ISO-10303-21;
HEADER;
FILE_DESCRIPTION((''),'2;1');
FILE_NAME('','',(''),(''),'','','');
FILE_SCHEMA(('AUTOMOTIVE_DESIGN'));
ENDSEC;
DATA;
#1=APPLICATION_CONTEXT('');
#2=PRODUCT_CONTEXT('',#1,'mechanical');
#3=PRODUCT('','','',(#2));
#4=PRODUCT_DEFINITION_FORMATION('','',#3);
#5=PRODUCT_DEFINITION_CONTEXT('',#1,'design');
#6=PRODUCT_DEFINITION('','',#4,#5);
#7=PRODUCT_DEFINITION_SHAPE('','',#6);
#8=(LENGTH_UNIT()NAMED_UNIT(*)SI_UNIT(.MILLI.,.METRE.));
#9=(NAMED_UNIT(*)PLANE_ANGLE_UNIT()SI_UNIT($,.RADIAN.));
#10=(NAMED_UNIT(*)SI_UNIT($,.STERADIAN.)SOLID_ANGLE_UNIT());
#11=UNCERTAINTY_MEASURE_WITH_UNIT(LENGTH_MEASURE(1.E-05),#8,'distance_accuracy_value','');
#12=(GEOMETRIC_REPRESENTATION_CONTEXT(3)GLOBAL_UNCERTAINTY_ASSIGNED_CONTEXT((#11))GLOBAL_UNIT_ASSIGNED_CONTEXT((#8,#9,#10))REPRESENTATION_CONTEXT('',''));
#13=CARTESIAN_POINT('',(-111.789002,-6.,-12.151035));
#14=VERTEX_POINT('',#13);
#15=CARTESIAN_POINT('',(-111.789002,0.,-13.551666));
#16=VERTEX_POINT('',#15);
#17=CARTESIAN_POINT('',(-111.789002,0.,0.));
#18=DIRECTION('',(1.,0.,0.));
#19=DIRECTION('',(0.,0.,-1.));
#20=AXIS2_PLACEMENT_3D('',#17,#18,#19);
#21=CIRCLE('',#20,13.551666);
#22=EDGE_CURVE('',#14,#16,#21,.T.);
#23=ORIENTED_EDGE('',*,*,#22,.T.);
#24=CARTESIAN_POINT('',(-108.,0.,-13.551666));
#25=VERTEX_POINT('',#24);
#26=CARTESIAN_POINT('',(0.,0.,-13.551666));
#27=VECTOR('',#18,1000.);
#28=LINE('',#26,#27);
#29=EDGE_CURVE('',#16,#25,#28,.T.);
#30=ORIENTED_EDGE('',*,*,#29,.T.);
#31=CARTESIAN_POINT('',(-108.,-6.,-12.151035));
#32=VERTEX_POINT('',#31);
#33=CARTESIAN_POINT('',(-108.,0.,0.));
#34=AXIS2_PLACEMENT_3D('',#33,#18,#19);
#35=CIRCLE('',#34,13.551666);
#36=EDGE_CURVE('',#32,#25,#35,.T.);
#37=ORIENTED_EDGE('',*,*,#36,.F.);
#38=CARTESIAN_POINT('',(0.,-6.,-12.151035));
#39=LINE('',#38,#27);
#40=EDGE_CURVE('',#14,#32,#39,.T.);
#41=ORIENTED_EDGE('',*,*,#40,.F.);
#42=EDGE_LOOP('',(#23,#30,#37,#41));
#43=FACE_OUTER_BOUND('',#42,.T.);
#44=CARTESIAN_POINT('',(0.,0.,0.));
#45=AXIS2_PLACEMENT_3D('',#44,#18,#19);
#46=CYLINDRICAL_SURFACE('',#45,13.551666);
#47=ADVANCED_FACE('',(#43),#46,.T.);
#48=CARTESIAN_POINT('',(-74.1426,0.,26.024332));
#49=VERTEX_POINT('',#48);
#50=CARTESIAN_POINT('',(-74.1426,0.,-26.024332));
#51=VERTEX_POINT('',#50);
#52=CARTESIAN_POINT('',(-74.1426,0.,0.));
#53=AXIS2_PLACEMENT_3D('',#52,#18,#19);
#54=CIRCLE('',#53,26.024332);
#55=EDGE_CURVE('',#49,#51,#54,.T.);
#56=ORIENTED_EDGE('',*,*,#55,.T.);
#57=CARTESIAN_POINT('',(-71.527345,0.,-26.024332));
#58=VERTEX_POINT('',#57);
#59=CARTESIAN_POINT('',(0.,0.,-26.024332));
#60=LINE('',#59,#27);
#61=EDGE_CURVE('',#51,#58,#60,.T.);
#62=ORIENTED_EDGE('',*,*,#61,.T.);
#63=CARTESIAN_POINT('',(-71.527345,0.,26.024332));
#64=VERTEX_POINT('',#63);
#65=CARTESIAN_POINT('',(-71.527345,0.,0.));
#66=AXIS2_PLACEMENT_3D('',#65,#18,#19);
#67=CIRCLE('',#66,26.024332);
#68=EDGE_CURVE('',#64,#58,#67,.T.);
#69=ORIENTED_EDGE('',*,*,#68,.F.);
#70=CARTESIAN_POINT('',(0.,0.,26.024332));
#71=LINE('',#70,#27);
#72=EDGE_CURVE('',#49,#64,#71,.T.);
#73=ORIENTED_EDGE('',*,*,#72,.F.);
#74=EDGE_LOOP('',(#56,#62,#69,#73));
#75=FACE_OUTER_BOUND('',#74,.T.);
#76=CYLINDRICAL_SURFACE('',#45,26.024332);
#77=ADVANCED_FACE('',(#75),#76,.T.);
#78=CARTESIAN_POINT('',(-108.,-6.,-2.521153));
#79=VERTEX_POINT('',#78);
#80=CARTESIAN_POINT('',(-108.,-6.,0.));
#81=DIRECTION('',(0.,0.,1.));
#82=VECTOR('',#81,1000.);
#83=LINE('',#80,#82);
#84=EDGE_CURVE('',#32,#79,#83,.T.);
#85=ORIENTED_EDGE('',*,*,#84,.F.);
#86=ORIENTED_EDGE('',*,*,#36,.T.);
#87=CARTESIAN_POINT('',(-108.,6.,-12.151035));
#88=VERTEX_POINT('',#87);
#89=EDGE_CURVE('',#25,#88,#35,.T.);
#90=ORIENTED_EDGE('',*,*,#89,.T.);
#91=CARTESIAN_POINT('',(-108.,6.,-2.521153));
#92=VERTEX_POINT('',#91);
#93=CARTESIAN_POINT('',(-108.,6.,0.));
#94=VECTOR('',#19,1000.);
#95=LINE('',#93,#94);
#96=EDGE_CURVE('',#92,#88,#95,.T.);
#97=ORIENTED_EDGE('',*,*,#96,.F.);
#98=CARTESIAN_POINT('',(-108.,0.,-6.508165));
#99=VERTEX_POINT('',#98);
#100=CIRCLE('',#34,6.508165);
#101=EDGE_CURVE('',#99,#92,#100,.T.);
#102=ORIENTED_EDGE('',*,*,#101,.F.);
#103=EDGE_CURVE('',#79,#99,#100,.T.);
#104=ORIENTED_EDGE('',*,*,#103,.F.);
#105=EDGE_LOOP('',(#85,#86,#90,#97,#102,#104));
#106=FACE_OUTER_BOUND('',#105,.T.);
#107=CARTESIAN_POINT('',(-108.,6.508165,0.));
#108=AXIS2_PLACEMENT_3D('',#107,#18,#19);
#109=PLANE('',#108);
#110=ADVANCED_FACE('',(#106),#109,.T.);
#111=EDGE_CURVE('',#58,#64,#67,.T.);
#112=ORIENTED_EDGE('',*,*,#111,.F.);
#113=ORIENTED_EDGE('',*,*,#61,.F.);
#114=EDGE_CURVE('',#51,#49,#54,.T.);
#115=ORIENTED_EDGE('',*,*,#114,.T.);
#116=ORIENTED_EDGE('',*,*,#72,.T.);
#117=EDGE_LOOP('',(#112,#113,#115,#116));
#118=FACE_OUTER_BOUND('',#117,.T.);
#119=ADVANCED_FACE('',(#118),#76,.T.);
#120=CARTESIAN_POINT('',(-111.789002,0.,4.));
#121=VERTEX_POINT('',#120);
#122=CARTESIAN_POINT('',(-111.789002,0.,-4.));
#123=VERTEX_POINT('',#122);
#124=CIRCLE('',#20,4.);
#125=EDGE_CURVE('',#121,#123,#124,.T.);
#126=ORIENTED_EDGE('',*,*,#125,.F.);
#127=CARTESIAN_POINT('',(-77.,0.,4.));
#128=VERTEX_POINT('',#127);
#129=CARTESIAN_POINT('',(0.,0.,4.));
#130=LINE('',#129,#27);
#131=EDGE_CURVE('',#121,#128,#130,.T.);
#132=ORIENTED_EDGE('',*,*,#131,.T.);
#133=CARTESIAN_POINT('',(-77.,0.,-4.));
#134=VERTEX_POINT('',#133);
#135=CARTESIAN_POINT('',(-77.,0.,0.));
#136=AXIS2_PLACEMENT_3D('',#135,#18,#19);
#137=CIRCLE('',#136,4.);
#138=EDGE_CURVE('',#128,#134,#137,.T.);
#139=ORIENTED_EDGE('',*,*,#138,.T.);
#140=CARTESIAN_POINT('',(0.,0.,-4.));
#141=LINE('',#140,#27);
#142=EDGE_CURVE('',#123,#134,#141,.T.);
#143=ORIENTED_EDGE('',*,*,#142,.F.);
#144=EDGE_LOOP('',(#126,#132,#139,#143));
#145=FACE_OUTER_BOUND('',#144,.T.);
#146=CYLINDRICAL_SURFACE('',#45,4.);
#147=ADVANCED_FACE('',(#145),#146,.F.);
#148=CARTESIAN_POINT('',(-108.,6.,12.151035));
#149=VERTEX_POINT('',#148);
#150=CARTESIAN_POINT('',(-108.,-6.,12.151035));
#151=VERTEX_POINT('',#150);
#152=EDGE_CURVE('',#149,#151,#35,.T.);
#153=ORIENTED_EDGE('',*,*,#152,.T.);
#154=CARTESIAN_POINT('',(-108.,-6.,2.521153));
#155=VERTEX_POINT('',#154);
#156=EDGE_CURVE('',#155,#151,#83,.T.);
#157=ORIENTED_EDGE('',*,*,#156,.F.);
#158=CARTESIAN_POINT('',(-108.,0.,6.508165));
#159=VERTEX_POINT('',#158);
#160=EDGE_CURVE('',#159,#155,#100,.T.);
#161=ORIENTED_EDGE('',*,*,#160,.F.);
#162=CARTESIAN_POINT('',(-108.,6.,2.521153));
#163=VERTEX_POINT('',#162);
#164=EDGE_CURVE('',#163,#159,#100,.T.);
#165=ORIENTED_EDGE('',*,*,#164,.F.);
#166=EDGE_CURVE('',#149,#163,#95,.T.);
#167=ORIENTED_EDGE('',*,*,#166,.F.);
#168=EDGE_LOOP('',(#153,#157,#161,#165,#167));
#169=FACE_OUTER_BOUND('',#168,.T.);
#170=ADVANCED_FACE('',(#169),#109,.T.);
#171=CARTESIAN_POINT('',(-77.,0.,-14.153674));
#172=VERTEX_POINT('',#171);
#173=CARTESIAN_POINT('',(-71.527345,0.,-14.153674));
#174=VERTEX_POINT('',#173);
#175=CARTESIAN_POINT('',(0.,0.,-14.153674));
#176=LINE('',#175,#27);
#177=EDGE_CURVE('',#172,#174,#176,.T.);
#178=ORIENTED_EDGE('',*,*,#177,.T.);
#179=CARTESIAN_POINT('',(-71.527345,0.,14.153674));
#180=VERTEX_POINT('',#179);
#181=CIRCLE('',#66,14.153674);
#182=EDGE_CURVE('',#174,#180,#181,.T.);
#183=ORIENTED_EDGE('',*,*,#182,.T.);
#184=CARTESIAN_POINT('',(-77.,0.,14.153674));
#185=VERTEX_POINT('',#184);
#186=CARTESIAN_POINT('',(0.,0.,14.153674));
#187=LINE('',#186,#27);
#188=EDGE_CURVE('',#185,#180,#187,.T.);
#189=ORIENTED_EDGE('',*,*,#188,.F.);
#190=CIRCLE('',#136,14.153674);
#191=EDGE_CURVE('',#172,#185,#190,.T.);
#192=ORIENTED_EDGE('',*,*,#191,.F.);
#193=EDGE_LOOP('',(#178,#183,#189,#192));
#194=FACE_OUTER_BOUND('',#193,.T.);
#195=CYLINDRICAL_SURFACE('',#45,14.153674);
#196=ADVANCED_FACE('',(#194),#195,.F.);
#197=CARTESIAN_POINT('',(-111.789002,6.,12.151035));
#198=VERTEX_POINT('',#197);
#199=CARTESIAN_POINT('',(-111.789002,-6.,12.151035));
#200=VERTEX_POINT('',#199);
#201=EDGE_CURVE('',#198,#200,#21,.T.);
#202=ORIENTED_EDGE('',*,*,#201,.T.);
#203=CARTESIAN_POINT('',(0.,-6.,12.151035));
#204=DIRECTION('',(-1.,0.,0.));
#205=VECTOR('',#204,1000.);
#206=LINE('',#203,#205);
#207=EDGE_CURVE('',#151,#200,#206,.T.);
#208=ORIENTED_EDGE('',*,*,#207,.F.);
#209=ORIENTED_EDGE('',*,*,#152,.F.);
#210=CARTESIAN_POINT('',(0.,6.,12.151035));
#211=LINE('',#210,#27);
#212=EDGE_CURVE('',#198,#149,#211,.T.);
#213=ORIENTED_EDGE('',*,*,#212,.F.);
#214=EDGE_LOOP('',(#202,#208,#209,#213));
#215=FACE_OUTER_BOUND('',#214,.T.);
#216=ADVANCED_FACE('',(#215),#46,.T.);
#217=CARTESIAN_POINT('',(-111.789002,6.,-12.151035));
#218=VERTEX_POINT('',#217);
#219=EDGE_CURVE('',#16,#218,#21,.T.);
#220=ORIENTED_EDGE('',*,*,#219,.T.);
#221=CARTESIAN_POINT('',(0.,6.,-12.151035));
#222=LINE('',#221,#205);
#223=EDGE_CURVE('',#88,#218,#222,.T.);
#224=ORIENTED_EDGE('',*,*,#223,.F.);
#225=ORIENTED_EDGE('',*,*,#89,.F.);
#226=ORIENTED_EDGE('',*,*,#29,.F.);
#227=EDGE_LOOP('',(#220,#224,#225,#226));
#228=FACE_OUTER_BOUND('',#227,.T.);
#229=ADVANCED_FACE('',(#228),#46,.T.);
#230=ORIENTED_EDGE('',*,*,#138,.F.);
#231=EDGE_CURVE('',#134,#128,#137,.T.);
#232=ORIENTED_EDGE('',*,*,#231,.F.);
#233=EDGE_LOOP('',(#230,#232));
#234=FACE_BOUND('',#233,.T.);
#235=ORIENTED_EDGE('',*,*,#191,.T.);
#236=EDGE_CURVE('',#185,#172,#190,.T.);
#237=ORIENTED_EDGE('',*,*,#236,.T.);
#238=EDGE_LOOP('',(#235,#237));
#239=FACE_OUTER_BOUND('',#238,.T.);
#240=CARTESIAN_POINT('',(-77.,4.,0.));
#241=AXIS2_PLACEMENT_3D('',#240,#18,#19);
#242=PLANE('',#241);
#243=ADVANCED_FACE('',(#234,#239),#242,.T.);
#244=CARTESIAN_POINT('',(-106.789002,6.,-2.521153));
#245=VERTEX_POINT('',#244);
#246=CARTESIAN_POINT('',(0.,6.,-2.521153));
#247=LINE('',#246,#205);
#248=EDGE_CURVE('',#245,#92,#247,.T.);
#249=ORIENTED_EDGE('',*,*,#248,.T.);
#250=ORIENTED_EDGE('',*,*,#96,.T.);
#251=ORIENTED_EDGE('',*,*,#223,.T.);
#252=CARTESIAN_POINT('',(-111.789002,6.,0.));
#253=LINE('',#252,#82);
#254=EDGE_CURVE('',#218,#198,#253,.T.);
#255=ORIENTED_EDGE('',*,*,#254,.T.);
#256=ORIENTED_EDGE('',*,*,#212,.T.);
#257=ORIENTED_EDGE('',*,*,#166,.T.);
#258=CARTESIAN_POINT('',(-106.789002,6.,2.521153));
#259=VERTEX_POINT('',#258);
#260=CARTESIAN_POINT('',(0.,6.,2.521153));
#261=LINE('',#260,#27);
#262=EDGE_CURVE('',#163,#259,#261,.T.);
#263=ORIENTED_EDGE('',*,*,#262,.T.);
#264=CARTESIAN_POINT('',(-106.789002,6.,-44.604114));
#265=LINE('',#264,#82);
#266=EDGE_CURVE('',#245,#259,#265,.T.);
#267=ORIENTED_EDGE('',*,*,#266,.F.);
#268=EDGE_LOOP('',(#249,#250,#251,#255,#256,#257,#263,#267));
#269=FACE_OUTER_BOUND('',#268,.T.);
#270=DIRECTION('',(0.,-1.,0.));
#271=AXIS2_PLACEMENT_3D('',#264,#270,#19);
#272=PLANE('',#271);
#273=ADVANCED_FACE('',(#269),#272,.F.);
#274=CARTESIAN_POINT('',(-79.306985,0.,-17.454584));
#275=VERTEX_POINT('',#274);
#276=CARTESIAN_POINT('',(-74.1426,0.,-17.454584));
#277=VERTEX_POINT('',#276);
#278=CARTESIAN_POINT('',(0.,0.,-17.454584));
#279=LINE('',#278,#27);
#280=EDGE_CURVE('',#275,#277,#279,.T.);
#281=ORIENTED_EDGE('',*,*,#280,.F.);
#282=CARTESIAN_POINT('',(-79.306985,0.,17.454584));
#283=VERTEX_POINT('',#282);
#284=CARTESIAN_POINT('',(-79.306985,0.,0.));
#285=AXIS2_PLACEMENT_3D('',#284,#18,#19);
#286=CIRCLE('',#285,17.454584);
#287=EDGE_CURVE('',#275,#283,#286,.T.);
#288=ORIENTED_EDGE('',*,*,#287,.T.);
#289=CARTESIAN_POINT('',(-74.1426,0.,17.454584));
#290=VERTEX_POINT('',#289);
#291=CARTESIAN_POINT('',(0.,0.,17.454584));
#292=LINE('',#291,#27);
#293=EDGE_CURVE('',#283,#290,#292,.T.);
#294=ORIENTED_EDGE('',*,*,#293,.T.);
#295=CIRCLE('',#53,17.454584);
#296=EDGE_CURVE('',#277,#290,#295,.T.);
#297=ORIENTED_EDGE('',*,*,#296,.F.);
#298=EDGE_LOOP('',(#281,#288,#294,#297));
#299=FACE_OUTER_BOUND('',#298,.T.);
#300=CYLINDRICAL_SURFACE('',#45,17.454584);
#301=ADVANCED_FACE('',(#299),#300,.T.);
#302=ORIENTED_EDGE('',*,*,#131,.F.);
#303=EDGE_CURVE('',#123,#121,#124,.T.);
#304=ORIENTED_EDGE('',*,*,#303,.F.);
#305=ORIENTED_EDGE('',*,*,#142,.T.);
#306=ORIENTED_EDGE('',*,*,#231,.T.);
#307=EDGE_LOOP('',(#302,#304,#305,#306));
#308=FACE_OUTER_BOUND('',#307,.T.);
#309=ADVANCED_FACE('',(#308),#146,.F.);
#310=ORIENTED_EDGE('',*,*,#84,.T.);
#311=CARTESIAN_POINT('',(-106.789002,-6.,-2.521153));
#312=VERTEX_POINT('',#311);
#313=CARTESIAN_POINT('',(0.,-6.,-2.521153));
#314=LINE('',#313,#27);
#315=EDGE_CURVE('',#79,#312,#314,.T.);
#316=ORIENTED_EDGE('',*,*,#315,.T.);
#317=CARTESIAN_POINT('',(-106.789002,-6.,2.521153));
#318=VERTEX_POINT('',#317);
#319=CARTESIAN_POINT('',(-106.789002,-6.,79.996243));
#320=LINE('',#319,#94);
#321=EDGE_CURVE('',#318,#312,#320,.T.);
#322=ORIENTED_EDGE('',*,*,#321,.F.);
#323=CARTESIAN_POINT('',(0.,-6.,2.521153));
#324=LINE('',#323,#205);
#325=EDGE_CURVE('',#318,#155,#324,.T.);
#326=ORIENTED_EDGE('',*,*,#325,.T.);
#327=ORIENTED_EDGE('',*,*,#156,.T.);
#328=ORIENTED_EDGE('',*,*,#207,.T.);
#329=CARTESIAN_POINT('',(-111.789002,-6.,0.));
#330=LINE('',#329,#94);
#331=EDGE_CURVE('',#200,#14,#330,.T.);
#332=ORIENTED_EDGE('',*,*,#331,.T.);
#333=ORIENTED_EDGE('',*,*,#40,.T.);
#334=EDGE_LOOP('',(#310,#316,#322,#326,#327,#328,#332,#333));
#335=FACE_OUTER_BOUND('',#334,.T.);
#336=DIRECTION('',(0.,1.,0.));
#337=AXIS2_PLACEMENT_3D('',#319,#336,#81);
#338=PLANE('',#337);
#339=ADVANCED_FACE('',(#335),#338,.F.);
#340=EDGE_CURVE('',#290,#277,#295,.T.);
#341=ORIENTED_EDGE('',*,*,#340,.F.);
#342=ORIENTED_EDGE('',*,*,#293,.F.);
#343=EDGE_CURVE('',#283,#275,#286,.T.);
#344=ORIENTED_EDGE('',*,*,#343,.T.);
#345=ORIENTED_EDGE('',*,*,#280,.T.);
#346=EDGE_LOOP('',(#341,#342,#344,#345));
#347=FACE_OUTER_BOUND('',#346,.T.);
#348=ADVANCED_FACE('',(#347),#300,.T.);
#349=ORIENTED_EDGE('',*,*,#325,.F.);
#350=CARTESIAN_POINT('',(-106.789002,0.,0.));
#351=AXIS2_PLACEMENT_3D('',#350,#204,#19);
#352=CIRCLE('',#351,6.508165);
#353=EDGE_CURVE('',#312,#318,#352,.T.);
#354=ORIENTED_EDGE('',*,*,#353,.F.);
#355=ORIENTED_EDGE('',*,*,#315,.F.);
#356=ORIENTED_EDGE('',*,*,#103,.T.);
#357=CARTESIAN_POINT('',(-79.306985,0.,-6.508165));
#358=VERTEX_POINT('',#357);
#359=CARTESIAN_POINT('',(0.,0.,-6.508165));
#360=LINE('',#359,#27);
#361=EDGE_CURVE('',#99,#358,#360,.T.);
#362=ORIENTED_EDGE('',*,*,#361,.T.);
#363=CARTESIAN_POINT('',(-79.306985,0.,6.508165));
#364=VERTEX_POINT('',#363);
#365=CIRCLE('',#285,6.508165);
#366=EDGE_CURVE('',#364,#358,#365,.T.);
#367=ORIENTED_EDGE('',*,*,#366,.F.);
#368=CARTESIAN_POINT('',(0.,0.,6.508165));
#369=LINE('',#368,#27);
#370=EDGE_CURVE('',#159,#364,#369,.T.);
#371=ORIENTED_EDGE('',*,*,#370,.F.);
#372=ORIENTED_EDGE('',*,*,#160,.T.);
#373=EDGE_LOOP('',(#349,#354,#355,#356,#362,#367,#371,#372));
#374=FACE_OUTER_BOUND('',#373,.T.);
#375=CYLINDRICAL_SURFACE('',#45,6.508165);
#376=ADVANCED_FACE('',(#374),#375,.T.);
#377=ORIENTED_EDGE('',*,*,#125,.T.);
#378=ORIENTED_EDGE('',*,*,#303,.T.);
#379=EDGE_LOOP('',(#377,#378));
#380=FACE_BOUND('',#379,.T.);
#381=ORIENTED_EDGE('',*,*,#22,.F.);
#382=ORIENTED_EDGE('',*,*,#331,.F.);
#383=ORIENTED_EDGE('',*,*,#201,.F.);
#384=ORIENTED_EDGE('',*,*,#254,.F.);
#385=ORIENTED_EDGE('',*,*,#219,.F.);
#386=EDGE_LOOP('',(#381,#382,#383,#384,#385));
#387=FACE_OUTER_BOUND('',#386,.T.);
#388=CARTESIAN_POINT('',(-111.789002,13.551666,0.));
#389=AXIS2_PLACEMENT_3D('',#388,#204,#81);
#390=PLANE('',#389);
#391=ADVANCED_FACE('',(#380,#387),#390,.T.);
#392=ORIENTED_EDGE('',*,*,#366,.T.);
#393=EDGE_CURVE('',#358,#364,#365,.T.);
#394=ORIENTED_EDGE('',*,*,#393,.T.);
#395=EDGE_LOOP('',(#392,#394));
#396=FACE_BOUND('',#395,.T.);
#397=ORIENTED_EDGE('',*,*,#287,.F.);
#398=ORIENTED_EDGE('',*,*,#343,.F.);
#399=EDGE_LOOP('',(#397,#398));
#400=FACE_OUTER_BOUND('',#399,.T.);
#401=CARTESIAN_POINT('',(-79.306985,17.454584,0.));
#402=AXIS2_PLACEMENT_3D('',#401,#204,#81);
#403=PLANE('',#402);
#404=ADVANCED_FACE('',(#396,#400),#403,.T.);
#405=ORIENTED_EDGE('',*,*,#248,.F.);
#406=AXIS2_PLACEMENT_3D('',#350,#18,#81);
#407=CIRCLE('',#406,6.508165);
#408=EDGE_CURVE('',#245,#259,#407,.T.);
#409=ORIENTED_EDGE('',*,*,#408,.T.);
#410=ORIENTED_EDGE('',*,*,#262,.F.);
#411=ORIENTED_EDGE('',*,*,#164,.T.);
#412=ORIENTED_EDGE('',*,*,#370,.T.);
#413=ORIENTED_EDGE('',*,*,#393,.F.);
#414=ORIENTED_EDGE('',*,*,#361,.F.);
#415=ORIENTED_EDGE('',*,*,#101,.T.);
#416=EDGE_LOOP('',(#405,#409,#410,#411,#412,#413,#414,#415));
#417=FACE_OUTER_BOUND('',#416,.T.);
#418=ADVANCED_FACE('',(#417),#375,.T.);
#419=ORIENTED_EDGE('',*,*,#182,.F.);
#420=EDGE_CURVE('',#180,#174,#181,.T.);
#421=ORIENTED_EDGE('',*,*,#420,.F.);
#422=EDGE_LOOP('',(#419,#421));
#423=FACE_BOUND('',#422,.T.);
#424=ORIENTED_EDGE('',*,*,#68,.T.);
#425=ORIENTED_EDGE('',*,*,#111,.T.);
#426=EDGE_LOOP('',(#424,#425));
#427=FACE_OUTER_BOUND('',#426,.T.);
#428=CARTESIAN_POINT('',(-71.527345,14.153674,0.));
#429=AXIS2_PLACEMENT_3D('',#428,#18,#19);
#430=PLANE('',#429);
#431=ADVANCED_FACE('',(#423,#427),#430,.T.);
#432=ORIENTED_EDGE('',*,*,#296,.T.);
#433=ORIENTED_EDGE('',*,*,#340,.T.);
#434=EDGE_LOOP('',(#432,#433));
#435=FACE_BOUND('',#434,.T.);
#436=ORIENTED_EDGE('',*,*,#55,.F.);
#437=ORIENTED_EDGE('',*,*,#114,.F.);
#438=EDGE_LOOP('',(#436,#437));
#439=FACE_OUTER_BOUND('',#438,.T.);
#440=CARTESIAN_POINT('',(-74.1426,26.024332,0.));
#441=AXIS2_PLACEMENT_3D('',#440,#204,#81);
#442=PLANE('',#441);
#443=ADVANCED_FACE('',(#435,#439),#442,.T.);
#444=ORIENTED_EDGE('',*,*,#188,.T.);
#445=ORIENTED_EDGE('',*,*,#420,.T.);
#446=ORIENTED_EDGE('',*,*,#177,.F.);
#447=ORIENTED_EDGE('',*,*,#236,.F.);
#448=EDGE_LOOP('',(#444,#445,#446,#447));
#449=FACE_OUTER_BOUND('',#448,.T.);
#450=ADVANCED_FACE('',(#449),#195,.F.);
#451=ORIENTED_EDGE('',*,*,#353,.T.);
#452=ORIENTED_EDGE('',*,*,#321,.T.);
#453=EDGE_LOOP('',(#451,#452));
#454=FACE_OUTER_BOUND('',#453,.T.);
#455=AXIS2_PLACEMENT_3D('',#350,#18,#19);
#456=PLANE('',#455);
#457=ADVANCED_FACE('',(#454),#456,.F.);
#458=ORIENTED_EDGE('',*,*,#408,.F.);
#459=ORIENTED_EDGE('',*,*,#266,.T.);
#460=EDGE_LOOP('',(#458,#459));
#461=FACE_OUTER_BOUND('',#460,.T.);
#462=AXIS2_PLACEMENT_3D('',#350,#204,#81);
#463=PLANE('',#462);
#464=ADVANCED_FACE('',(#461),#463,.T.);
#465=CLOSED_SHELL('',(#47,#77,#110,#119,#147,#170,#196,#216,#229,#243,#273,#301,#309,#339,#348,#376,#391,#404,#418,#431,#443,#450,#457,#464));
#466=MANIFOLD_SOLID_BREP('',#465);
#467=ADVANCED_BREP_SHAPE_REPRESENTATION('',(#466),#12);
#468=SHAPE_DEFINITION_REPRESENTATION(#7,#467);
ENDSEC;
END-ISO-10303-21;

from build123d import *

# Parameters (mm, degrees)
SKETCH2_W          = 82.566044685
SKETCH2_H          = 15.592809798
SKETCH2_W_2        = 148.96712198
SKETCH2_H_2        = 11.958140401
CUT_EXTRUDE1_DEPTH = 5


with BuildPart() as part:
    # Sketch1 → Revolve1 (revolve)
    with BuildSketch(Plane.XY, mode=Mode.PRIVATE) as revolve1_sk:
        Polygon((-74.14259961, 26.024332396), (-74.14259961, 17.45458405), (-79.306985444, 17.45458405), (-79.306985444, 6.508165042), (-108, 6.508165042), (-108, 13.551665989), (-109.954236571, 13.551665989), (-111.789002112, 13.551665989), (-111.789002112, 4), (-106.267464057, 4), (-77, 4), (-77, 14.153673902), (-71.527344849, 14.153673902), (-71.527344849, 26.024332396), align=None)
    revolve(revolve1_sk.sketch.rotate(Axis((0, 0, 0), (-1, 0, 0)), 90), axis=Axis((0, 0, 0), (-1, 0, 0)))

    # Sketch2 → Cut-Extrude1 (cut)
    with BuildSketch(Plane.ZY.offset(111.789002112)):
        with Locations((-3.321091868, 13.796404899)):
            Rectangle(SKETCH2_W, SKETCH2_H)
        with Locations((5.512682346, -11.979070201)):
            Rectangle(SKETCH2_W_2, SKETCH2_H_2)
    extrude(amount=-CUT_EXTRUDE1_DEPTH, mode=Mode.SUBTRACT)


solid = part.part
